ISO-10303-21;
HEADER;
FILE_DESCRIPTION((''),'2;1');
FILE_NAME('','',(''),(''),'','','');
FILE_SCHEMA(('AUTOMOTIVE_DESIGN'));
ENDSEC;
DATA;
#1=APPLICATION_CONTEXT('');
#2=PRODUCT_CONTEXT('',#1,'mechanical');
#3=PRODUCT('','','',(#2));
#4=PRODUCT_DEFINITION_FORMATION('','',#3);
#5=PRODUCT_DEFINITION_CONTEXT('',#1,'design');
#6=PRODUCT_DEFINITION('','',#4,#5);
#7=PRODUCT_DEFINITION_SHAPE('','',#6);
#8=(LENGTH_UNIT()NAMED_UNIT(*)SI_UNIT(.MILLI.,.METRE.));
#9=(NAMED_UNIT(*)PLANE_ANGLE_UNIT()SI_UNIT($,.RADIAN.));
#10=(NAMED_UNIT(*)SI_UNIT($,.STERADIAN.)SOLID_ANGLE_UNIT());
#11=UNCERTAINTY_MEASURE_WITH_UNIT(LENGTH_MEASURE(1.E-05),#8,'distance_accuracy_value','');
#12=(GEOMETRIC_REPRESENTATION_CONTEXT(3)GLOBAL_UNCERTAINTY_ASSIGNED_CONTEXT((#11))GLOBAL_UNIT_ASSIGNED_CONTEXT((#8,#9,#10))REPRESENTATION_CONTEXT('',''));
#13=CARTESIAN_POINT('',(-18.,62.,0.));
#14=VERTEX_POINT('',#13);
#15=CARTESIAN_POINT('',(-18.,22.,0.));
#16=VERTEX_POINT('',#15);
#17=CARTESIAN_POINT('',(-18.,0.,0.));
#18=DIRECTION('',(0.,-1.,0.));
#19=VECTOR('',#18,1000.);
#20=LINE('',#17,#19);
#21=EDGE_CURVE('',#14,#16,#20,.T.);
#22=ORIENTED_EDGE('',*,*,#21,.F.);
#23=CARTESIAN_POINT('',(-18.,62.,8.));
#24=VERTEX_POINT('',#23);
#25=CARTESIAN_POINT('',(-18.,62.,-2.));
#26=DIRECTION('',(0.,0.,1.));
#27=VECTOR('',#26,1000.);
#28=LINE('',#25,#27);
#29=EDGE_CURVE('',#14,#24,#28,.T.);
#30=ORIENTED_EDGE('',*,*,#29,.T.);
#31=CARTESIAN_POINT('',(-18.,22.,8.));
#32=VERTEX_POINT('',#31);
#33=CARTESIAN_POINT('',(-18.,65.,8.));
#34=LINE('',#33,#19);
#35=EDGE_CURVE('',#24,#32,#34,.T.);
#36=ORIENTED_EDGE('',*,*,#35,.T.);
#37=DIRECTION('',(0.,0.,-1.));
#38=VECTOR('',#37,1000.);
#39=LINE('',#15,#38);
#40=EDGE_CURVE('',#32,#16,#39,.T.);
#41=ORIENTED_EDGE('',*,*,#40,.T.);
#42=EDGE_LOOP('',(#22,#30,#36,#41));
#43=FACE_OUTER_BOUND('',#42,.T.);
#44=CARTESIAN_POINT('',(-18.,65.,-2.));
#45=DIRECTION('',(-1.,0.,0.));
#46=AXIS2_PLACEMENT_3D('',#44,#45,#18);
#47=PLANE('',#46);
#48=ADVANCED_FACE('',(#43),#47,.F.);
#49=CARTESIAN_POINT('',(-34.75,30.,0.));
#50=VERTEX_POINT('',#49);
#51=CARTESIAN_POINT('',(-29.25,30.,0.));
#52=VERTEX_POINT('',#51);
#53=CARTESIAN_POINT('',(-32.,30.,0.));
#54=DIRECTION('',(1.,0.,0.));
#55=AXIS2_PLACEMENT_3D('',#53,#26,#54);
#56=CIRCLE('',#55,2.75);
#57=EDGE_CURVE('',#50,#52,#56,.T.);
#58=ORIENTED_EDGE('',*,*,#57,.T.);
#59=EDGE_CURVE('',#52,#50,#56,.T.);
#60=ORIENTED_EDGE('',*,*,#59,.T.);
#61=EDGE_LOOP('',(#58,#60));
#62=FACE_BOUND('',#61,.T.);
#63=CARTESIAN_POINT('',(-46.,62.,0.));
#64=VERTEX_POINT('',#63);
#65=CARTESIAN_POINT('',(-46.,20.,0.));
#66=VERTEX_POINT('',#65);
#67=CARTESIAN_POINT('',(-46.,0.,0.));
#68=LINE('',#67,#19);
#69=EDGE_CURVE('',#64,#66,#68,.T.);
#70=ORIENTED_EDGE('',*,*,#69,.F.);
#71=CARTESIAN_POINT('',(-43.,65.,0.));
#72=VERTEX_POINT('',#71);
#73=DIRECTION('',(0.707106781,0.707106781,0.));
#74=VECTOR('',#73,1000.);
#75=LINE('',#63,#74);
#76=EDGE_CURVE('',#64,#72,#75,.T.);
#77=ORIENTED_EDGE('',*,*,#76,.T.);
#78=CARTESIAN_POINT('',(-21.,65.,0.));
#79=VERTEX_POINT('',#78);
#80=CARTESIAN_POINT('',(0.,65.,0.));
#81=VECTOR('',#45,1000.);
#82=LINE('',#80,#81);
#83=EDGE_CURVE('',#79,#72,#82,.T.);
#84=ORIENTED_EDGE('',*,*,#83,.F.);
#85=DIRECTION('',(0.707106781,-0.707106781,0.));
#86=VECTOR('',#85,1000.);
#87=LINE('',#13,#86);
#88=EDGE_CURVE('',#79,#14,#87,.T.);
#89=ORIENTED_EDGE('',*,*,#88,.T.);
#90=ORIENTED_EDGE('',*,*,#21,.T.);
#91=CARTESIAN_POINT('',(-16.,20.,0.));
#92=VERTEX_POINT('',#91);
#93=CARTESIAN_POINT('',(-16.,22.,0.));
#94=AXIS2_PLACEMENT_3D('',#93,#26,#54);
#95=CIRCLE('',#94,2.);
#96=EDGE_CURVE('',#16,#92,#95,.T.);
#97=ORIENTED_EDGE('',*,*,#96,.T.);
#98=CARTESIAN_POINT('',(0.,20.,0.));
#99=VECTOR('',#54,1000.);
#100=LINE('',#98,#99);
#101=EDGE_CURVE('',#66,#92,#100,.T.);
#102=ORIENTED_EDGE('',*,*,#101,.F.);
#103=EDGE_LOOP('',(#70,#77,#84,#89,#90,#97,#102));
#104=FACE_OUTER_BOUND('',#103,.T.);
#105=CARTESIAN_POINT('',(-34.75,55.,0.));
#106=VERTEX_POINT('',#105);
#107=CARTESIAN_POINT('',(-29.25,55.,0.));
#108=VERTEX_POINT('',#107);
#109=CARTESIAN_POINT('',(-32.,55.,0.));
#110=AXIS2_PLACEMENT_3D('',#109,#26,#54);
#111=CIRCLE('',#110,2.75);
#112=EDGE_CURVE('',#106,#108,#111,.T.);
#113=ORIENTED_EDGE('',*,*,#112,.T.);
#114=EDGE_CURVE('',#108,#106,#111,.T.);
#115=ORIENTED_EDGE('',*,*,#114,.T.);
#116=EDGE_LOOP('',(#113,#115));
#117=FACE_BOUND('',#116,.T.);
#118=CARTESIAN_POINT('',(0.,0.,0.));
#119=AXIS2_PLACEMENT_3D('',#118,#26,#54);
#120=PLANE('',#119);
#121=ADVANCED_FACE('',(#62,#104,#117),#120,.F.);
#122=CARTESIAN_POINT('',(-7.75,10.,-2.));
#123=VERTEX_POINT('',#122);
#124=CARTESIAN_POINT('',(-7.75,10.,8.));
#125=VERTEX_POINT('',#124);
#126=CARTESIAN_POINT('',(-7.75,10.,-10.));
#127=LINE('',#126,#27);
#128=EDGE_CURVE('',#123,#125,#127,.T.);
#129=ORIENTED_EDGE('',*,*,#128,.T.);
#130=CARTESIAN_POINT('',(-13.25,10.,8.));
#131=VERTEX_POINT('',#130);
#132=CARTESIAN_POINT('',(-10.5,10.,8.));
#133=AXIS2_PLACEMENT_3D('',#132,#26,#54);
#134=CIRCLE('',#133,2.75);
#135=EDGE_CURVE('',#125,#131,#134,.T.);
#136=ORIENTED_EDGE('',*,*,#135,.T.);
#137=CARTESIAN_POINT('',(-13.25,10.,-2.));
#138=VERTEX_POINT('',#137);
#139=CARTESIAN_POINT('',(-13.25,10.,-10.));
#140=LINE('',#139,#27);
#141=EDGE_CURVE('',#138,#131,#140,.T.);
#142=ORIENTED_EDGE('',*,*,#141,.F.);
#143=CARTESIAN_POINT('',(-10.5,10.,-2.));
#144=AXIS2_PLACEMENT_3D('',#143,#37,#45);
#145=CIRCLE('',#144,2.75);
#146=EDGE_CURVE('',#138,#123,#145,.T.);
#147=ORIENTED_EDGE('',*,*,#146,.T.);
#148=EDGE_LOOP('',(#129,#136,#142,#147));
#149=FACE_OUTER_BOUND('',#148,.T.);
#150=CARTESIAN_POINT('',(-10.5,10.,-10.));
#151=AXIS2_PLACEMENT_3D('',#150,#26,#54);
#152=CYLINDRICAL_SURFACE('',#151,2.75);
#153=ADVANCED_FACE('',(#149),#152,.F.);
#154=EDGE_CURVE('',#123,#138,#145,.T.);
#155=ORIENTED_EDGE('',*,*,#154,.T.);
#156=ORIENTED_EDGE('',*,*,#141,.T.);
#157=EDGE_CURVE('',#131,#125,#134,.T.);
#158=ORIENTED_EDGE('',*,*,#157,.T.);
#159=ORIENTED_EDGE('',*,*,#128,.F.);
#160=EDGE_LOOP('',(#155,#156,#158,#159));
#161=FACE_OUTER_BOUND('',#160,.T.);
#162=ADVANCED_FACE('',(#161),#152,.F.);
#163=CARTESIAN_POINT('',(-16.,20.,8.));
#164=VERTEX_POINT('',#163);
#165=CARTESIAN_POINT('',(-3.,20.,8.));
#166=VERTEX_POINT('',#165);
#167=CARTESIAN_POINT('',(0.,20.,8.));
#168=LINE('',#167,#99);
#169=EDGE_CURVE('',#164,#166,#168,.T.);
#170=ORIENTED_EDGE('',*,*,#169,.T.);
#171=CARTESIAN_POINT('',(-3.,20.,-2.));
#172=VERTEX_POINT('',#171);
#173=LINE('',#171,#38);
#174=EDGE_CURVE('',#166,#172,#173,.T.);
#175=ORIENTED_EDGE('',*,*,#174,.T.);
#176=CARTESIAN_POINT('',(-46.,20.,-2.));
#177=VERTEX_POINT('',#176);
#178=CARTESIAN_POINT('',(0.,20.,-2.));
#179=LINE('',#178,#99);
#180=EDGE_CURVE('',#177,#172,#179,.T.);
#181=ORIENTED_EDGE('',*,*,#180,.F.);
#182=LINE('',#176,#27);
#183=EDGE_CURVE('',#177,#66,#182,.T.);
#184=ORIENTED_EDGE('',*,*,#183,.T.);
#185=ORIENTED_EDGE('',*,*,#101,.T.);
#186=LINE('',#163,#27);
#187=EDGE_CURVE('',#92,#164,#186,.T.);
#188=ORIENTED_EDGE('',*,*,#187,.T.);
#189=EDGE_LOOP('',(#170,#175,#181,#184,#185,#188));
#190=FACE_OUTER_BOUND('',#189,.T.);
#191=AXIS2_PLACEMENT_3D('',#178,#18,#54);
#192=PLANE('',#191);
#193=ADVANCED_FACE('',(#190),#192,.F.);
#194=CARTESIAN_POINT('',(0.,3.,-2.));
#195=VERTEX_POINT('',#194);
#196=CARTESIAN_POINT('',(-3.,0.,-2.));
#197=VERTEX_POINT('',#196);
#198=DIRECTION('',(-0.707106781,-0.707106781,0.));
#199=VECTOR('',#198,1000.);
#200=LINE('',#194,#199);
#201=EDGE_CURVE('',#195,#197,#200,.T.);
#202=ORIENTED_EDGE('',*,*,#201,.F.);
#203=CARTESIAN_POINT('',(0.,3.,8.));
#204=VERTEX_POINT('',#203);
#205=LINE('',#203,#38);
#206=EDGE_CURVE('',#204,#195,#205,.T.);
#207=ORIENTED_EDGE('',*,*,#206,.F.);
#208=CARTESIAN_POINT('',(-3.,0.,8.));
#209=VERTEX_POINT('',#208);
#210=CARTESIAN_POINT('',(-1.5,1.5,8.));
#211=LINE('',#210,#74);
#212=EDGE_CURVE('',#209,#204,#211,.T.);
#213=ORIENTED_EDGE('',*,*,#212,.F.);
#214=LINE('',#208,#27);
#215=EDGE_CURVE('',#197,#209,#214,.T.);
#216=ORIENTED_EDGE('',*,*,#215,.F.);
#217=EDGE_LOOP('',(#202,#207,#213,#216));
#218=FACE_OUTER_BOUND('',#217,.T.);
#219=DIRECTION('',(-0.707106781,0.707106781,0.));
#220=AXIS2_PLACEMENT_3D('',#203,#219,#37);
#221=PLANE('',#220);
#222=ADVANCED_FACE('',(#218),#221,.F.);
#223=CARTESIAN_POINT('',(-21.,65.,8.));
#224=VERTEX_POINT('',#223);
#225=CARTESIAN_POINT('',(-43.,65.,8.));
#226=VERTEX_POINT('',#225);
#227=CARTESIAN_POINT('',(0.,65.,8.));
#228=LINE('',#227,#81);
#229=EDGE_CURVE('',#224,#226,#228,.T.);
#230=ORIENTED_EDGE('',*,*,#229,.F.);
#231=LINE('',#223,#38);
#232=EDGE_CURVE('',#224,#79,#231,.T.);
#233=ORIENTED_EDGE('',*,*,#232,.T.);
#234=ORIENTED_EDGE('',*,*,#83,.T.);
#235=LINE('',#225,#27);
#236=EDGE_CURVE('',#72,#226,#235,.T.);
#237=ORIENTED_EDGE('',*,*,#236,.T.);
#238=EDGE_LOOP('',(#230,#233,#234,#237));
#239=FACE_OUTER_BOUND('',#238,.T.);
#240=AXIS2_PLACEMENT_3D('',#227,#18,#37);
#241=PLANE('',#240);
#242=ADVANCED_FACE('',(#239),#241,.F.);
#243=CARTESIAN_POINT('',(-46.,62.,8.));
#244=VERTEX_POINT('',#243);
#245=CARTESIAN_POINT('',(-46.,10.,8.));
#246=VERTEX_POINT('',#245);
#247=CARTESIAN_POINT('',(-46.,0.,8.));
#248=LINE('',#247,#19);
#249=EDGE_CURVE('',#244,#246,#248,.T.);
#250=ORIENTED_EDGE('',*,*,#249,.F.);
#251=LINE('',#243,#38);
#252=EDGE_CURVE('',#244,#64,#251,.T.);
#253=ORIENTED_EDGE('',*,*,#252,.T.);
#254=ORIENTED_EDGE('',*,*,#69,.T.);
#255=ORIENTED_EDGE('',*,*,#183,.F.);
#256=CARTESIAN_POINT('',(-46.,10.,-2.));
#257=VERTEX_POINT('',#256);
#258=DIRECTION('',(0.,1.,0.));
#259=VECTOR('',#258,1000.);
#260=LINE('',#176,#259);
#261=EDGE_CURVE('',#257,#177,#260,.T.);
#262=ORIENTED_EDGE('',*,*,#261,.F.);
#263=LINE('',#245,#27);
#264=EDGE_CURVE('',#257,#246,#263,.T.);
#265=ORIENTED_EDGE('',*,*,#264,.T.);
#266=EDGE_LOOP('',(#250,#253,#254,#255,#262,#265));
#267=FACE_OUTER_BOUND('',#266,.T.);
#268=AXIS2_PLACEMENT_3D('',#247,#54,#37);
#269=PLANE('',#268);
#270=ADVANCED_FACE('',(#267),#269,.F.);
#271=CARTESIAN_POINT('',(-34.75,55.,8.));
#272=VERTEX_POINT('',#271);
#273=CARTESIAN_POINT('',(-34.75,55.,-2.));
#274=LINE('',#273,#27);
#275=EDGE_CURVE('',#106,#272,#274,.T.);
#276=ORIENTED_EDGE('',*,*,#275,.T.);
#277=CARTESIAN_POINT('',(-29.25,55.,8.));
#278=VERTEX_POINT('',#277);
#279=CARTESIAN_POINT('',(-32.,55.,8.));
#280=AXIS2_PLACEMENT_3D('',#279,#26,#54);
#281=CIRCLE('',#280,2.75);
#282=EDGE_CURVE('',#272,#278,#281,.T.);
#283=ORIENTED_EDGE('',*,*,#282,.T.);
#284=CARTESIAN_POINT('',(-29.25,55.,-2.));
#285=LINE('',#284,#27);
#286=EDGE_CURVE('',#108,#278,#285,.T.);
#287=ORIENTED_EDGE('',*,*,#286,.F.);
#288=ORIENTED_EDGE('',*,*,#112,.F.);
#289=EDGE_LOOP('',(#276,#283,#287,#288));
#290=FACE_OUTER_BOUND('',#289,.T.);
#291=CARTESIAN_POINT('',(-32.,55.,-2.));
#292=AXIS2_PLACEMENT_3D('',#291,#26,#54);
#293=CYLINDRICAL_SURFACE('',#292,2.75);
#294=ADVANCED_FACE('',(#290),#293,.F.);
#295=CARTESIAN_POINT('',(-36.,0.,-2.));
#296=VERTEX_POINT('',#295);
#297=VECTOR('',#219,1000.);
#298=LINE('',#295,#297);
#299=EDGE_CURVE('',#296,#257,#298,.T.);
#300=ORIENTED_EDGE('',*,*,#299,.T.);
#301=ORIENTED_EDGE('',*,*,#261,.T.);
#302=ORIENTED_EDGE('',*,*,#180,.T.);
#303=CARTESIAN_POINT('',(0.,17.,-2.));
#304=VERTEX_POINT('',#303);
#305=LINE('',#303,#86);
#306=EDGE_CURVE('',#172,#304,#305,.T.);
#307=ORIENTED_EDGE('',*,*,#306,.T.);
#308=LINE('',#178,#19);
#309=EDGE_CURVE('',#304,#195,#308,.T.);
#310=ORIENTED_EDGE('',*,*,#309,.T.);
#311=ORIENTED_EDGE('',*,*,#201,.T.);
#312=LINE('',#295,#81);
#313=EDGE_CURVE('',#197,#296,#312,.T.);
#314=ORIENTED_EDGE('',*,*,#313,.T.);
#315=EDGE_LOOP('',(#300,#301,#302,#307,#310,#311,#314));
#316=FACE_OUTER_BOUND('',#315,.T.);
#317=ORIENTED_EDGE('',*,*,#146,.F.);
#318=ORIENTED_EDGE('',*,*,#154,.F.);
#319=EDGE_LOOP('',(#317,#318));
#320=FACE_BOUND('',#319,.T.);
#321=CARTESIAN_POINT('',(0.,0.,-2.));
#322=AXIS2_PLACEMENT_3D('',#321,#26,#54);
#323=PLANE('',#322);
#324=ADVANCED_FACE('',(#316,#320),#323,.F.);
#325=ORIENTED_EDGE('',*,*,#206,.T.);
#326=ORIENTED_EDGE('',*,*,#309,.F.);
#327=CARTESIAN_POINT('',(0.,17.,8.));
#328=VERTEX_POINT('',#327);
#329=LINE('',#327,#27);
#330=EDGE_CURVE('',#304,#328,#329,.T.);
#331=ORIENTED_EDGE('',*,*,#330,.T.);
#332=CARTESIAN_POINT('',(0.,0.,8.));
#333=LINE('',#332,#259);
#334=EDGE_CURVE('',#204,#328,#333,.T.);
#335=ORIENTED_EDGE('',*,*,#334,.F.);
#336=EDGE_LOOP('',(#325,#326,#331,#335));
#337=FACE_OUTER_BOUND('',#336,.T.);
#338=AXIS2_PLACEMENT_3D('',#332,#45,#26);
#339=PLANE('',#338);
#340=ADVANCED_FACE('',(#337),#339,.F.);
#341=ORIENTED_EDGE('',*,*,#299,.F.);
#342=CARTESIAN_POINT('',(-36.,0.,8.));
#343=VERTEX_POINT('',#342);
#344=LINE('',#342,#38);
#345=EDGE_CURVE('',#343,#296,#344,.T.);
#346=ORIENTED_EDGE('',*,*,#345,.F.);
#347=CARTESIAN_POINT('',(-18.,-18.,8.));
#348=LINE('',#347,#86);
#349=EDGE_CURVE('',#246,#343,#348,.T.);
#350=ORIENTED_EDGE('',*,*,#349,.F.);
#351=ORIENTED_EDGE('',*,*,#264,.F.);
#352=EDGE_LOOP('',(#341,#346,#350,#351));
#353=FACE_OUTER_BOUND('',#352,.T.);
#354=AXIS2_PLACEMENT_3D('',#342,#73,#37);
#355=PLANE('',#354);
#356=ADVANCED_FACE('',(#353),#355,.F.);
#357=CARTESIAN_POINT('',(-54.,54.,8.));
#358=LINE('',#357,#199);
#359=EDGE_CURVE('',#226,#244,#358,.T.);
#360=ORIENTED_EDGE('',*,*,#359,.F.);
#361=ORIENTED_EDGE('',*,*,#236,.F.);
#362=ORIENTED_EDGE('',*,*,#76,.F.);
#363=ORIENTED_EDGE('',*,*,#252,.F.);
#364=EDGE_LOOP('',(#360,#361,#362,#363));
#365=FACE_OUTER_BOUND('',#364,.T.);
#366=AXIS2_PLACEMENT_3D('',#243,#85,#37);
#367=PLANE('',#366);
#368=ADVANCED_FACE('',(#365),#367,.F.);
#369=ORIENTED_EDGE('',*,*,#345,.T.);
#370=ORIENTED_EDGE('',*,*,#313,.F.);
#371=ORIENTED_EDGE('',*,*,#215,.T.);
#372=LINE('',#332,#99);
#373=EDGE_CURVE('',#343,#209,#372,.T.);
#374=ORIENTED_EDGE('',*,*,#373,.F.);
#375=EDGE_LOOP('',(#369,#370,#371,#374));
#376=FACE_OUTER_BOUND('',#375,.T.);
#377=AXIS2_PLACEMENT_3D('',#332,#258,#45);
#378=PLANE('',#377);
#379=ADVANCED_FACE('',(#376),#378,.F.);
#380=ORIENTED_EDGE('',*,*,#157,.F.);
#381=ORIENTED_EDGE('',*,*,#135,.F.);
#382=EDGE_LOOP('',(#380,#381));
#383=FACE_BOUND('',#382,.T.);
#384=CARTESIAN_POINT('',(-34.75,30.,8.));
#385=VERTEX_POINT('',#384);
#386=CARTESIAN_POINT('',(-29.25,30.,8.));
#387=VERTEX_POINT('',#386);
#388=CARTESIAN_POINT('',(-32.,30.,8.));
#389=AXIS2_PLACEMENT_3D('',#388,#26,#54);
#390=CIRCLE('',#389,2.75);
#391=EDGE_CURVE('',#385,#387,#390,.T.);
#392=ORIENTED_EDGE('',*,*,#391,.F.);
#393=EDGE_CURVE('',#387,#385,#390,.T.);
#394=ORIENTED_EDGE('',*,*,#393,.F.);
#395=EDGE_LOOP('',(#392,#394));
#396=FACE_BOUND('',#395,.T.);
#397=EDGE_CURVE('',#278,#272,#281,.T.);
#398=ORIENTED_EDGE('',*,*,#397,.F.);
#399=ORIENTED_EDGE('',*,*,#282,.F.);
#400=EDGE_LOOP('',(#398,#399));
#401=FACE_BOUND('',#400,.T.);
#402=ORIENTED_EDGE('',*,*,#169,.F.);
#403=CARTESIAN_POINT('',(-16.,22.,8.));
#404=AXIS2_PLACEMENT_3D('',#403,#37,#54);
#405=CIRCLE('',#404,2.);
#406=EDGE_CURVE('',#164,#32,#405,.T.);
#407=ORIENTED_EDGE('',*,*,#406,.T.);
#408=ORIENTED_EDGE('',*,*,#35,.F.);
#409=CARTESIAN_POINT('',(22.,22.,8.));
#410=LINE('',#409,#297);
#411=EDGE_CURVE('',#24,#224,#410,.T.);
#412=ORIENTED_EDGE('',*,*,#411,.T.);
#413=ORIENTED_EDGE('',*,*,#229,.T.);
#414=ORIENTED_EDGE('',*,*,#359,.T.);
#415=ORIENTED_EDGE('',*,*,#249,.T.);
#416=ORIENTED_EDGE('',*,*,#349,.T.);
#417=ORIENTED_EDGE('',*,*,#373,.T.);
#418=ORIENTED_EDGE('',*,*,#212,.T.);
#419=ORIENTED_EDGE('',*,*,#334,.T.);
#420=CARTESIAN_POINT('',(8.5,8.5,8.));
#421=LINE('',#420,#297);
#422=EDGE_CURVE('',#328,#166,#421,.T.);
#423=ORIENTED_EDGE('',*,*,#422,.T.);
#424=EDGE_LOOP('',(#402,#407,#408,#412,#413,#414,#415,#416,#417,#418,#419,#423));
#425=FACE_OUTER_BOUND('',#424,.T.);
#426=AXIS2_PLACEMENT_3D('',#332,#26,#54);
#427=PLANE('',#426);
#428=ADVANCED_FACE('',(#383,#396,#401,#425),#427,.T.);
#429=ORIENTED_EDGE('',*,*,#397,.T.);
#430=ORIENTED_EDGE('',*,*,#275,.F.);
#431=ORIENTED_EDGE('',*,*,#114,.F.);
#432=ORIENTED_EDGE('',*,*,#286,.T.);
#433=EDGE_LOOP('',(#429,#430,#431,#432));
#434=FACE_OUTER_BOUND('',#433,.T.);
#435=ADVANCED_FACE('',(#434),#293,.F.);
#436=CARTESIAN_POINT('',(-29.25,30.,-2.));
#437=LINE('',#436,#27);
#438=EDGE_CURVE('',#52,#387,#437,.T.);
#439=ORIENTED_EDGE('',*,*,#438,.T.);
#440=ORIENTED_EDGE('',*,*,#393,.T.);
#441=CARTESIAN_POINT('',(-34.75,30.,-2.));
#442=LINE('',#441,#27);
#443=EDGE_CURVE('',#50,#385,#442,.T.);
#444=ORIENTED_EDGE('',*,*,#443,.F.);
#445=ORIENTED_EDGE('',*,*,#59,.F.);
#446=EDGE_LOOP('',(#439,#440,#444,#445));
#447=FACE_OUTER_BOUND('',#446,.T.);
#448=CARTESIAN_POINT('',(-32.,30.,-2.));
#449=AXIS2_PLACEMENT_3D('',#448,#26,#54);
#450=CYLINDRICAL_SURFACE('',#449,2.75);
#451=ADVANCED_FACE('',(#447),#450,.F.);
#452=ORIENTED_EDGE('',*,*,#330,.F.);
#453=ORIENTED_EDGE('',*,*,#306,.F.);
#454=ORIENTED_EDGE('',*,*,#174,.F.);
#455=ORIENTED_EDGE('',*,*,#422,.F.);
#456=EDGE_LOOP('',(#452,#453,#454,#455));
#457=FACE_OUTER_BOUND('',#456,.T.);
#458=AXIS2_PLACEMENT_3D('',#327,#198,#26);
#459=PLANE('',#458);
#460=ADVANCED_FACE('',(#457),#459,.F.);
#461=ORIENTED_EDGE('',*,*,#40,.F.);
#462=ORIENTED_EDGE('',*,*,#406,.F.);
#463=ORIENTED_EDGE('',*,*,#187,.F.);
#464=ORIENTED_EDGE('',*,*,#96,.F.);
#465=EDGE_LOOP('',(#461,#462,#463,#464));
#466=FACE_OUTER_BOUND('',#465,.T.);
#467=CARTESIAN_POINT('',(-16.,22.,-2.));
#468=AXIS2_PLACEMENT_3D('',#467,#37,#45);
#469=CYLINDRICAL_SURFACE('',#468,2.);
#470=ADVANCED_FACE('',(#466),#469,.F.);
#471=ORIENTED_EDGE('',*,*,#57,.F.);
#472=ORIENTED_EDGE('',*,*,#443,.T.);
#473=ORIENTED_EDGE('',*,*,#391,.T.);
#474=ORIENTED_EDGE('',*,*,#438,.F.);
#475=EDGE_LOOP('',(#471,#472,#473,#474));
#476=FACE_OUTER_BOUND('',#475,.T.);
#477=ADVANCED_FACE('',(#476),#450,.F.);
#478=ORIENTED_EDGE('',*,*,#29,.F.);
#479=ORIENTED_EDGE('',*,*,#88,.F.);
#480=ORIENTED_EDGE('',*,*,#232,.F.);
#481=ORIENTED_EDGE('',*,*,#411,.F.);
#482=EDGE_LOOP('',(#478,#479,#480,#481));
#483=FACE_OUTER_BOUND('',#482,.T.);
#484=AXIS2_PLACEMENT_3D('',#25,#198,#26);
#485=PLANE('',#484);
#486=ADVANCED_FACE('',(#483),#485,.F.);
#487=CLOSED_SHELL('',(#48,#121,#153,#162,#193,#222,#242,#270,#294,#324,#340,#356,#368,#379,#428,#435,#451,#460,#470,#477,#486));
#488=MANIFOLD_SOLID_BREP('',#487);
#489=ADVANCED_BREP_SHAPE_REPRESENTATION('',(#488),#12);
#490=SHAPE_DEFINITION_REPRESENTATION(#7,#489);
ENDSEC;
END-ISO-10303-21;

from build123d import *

# Parameters (mm, degrees)
SKETCH1_W           = 46
SKETCH1_H           = 65
BOSS_EXTRUDE1_DEPTH = 8
SKETCH2_R           = 2.75
CUT_EXTRUDE1_DEPTH  = 18
CHAMFER1_SIZE       = 10
SKETCH3_R           = 2.75
CUT_EXTRUDE2_DEPTH  = 10
SKETCH4_W           = 18
SKETCH4_H           = 45
CUT_EXTRUDE3_DEPTH  = 10
SKETCH5_R           = 2.75
BOSS_EXTRUDE2_DEPTH = 2
FILLET1_R           = 2
CHAMFER2_SIZE       = 3


with BuildPart() as part:
    # Sketch1 → Boss-Extrude1 (new body)
    with BuildSketch(Plane.XY):
        with Locations((-23, 32.5)):
            Rectangle(SKETCH1_W, SKETCH1_H)
    extrude(amount=BOSS_EXTRUDE1_DEPTH)

    # Sketch2 → Cut-Extrude1 (cut)
    with BuildSketch(Plane.XY.offset(8)):
        with Locations((-10.5, 10)):
            Circle(SKETCH2_R)
    extrude(amount=-CUT_EXTRUDE1_DEPTH, mode=Mode.SUBTRACT)

    # Chamfer1
    chamfer1_edges = [part.edges().sort_by_distance(p)[0] for p in [
        (-46, 0, 4),
    ]]
    chamfer(chamfer1_edges, length=CHAMFER1_SIZE)

    # Sketch3 → Cut-Extrude2 (cut)
    with BuildSketch(Plane.XY.offset(8)):
        with Locations((-32, 55)):
            Circle(SKETCH3_R)
        with Locations((-32, 30)):
            Circle(SKETCH3_R)
    extrude(amount=-CUT_EXTRUDE2_DEPTH, mode=Mode.SUBTRACT)

    # Sketch4 → Cut-Extrude3 (cut)
    with BuildSketch(Plane.XY.offset(8)):
        with Locations((-9, 42.5)):
            Rectangle(SKETCH4_W, SKETCH4_H)
    extrude(amount=-CUT_EXTRUDE3_DEPTH, mode=Mode.SUBTRACT)

    # Sketch5 → Boss-Extrude2 (add)
    with BuildSketch(Plane(origin=(0, 0, 0), x_dir=(-1, 0, 0), z_dir=(0, 0, -1))):
        Polygon((0, 20), (46, 20), (46, 10), (36, 0), (0, 0), align=None)
        with Locations(Location((10.5, 10, 0), (0, 0, 180))):
            Circle(SKETCH5_R, mode=Mode.SUBTRACT)
    extrude(amount=BOSS_EXTRUDE2_DEPTH)

    # Fillet1
    fillet1_edges = [part.edges().sort_by_distance(p)[0] for p in [
        (-18, 20, 4),
    ]]
    fillet(fillet1_edges, radius=FILLET1_R)

    # Chamfer2
    chamfer2_edges = [part.edges().sort_by_distance(p)[0] for p in [
        (0, 0, 3),
        (0, 20, 3),
        (-18, 65, 4),
        (-46, 65, 4),
    ]]
    chamfer(chamfer2_edges, length=CHAMFER2_SIZE)


solid = part.part
